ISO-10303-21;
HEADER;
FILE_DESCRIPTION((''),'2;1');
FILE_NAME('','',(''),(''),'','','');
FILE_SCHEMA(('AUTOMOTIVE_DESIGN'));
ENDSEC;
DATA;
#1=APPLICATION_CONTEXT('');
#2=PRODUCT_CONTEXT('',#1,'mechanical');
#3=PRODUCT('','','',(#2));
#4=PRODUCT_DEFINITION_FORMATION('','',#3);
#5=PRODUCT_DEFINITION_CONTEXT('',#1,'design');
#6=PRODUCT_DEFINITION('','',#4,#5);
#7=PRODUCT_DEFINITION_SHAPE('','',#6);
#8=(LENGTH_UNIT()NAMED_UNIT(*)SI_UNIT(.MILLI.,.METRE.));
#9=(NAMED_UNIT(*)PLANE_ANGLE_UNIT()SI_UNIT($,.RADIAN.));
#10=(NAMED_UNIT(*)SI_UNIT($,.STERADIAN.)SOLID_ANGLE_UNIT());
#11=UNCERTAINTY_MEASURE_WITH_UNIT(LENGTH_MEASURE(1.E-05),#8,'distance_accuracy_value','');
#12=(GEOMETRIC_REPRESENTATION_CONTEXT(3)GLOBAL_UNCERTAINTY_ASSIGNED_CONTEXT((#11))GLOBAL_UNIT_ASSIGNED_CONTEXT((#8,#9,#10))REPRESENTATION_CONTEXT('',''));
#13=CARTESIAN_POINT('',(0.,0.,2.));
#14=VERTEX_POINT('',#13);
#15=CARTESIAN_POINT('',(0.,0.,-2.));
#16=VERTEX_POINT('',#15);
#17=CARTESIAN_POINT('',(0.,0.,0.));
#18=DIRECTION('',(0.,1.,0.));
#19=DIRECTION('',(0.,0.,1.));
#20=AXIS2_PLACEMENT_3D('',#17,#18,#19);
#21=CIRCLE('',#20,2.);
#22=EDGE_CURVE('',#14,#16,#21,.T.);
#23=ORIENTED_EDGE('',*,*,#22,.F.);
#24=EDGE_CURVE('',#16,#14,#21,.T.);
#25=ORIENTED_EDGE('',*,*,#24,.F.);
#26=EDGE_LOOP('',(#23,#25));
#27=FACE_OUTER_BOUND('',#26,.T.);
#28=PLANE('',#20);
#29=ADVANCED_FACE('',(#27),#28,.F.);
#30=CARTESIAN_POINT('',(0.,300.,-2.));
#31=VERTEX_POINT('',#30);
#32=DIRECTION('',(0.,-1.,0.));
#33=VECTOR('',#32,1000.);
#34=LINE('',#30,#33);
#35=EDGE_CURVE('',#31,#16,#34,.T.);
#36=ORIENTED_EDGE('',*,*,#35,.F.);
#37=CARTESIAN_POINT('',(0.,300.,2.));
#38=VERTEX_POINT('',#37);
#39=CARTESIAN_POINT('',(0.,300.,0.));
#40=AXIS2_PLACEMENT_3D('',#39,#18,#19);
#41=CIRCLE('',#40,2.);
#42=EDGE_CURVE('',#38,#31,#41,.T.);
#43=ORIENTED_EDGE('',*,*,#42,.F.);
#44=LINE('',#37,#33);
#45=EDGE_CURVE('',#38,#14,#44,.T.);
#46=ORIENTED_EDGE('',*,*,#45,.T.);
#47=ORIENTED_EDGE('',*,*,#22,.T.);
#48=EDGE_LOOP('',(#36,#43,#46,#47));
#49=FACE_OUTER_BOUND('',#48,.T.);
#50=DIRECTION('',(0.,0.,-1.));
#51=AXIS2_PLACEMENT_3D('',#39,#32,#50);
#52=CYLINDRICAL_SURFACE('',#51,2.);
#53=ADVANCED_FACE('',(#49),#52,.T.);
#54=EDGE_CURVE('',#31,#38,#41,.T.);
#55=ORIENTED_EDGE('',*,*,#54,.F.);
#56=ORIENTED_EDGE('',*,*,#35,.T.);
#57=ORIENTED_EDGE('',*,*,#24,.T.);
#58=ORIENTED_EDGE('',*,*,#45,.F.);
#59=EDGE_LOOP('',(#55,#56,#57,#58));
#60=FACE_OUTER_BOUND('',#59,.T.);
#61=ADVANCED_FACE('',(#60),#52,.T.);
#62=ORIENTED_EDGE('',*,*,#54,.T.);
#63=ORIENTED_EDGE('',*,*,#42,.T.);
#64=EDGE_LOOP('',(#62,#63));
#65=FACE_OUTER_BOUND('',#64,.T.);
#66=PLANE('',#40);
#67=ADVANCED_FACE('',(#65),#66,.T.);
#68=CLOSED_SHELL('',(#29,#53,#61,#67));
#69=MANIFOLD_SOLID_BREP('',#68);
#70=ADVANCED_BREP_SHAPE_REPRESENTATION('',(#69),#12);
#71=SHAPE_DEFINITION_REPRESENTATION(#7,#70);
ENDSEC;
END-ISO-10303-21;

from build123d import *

# Parameters (mm, degrees)
SKETCH_1_R      = 2
EXTRUDE_1_DEPTH = 300


with BuildPart() as part:
    # 草图1 → 凸台-拉伸1 (new body)
    with BuildSketch(Plane(origin=(0, 0, 0), x_dir=(1, 0, 0), z_dir=(0, 1, 0))):
        with Locations(Location((0, 0, 0), (0, 0, 270))):
            Circle(SKETCH_1_R)
    extrude(amount=EXTRUDE_1_DEPTH)


solid = part.part
